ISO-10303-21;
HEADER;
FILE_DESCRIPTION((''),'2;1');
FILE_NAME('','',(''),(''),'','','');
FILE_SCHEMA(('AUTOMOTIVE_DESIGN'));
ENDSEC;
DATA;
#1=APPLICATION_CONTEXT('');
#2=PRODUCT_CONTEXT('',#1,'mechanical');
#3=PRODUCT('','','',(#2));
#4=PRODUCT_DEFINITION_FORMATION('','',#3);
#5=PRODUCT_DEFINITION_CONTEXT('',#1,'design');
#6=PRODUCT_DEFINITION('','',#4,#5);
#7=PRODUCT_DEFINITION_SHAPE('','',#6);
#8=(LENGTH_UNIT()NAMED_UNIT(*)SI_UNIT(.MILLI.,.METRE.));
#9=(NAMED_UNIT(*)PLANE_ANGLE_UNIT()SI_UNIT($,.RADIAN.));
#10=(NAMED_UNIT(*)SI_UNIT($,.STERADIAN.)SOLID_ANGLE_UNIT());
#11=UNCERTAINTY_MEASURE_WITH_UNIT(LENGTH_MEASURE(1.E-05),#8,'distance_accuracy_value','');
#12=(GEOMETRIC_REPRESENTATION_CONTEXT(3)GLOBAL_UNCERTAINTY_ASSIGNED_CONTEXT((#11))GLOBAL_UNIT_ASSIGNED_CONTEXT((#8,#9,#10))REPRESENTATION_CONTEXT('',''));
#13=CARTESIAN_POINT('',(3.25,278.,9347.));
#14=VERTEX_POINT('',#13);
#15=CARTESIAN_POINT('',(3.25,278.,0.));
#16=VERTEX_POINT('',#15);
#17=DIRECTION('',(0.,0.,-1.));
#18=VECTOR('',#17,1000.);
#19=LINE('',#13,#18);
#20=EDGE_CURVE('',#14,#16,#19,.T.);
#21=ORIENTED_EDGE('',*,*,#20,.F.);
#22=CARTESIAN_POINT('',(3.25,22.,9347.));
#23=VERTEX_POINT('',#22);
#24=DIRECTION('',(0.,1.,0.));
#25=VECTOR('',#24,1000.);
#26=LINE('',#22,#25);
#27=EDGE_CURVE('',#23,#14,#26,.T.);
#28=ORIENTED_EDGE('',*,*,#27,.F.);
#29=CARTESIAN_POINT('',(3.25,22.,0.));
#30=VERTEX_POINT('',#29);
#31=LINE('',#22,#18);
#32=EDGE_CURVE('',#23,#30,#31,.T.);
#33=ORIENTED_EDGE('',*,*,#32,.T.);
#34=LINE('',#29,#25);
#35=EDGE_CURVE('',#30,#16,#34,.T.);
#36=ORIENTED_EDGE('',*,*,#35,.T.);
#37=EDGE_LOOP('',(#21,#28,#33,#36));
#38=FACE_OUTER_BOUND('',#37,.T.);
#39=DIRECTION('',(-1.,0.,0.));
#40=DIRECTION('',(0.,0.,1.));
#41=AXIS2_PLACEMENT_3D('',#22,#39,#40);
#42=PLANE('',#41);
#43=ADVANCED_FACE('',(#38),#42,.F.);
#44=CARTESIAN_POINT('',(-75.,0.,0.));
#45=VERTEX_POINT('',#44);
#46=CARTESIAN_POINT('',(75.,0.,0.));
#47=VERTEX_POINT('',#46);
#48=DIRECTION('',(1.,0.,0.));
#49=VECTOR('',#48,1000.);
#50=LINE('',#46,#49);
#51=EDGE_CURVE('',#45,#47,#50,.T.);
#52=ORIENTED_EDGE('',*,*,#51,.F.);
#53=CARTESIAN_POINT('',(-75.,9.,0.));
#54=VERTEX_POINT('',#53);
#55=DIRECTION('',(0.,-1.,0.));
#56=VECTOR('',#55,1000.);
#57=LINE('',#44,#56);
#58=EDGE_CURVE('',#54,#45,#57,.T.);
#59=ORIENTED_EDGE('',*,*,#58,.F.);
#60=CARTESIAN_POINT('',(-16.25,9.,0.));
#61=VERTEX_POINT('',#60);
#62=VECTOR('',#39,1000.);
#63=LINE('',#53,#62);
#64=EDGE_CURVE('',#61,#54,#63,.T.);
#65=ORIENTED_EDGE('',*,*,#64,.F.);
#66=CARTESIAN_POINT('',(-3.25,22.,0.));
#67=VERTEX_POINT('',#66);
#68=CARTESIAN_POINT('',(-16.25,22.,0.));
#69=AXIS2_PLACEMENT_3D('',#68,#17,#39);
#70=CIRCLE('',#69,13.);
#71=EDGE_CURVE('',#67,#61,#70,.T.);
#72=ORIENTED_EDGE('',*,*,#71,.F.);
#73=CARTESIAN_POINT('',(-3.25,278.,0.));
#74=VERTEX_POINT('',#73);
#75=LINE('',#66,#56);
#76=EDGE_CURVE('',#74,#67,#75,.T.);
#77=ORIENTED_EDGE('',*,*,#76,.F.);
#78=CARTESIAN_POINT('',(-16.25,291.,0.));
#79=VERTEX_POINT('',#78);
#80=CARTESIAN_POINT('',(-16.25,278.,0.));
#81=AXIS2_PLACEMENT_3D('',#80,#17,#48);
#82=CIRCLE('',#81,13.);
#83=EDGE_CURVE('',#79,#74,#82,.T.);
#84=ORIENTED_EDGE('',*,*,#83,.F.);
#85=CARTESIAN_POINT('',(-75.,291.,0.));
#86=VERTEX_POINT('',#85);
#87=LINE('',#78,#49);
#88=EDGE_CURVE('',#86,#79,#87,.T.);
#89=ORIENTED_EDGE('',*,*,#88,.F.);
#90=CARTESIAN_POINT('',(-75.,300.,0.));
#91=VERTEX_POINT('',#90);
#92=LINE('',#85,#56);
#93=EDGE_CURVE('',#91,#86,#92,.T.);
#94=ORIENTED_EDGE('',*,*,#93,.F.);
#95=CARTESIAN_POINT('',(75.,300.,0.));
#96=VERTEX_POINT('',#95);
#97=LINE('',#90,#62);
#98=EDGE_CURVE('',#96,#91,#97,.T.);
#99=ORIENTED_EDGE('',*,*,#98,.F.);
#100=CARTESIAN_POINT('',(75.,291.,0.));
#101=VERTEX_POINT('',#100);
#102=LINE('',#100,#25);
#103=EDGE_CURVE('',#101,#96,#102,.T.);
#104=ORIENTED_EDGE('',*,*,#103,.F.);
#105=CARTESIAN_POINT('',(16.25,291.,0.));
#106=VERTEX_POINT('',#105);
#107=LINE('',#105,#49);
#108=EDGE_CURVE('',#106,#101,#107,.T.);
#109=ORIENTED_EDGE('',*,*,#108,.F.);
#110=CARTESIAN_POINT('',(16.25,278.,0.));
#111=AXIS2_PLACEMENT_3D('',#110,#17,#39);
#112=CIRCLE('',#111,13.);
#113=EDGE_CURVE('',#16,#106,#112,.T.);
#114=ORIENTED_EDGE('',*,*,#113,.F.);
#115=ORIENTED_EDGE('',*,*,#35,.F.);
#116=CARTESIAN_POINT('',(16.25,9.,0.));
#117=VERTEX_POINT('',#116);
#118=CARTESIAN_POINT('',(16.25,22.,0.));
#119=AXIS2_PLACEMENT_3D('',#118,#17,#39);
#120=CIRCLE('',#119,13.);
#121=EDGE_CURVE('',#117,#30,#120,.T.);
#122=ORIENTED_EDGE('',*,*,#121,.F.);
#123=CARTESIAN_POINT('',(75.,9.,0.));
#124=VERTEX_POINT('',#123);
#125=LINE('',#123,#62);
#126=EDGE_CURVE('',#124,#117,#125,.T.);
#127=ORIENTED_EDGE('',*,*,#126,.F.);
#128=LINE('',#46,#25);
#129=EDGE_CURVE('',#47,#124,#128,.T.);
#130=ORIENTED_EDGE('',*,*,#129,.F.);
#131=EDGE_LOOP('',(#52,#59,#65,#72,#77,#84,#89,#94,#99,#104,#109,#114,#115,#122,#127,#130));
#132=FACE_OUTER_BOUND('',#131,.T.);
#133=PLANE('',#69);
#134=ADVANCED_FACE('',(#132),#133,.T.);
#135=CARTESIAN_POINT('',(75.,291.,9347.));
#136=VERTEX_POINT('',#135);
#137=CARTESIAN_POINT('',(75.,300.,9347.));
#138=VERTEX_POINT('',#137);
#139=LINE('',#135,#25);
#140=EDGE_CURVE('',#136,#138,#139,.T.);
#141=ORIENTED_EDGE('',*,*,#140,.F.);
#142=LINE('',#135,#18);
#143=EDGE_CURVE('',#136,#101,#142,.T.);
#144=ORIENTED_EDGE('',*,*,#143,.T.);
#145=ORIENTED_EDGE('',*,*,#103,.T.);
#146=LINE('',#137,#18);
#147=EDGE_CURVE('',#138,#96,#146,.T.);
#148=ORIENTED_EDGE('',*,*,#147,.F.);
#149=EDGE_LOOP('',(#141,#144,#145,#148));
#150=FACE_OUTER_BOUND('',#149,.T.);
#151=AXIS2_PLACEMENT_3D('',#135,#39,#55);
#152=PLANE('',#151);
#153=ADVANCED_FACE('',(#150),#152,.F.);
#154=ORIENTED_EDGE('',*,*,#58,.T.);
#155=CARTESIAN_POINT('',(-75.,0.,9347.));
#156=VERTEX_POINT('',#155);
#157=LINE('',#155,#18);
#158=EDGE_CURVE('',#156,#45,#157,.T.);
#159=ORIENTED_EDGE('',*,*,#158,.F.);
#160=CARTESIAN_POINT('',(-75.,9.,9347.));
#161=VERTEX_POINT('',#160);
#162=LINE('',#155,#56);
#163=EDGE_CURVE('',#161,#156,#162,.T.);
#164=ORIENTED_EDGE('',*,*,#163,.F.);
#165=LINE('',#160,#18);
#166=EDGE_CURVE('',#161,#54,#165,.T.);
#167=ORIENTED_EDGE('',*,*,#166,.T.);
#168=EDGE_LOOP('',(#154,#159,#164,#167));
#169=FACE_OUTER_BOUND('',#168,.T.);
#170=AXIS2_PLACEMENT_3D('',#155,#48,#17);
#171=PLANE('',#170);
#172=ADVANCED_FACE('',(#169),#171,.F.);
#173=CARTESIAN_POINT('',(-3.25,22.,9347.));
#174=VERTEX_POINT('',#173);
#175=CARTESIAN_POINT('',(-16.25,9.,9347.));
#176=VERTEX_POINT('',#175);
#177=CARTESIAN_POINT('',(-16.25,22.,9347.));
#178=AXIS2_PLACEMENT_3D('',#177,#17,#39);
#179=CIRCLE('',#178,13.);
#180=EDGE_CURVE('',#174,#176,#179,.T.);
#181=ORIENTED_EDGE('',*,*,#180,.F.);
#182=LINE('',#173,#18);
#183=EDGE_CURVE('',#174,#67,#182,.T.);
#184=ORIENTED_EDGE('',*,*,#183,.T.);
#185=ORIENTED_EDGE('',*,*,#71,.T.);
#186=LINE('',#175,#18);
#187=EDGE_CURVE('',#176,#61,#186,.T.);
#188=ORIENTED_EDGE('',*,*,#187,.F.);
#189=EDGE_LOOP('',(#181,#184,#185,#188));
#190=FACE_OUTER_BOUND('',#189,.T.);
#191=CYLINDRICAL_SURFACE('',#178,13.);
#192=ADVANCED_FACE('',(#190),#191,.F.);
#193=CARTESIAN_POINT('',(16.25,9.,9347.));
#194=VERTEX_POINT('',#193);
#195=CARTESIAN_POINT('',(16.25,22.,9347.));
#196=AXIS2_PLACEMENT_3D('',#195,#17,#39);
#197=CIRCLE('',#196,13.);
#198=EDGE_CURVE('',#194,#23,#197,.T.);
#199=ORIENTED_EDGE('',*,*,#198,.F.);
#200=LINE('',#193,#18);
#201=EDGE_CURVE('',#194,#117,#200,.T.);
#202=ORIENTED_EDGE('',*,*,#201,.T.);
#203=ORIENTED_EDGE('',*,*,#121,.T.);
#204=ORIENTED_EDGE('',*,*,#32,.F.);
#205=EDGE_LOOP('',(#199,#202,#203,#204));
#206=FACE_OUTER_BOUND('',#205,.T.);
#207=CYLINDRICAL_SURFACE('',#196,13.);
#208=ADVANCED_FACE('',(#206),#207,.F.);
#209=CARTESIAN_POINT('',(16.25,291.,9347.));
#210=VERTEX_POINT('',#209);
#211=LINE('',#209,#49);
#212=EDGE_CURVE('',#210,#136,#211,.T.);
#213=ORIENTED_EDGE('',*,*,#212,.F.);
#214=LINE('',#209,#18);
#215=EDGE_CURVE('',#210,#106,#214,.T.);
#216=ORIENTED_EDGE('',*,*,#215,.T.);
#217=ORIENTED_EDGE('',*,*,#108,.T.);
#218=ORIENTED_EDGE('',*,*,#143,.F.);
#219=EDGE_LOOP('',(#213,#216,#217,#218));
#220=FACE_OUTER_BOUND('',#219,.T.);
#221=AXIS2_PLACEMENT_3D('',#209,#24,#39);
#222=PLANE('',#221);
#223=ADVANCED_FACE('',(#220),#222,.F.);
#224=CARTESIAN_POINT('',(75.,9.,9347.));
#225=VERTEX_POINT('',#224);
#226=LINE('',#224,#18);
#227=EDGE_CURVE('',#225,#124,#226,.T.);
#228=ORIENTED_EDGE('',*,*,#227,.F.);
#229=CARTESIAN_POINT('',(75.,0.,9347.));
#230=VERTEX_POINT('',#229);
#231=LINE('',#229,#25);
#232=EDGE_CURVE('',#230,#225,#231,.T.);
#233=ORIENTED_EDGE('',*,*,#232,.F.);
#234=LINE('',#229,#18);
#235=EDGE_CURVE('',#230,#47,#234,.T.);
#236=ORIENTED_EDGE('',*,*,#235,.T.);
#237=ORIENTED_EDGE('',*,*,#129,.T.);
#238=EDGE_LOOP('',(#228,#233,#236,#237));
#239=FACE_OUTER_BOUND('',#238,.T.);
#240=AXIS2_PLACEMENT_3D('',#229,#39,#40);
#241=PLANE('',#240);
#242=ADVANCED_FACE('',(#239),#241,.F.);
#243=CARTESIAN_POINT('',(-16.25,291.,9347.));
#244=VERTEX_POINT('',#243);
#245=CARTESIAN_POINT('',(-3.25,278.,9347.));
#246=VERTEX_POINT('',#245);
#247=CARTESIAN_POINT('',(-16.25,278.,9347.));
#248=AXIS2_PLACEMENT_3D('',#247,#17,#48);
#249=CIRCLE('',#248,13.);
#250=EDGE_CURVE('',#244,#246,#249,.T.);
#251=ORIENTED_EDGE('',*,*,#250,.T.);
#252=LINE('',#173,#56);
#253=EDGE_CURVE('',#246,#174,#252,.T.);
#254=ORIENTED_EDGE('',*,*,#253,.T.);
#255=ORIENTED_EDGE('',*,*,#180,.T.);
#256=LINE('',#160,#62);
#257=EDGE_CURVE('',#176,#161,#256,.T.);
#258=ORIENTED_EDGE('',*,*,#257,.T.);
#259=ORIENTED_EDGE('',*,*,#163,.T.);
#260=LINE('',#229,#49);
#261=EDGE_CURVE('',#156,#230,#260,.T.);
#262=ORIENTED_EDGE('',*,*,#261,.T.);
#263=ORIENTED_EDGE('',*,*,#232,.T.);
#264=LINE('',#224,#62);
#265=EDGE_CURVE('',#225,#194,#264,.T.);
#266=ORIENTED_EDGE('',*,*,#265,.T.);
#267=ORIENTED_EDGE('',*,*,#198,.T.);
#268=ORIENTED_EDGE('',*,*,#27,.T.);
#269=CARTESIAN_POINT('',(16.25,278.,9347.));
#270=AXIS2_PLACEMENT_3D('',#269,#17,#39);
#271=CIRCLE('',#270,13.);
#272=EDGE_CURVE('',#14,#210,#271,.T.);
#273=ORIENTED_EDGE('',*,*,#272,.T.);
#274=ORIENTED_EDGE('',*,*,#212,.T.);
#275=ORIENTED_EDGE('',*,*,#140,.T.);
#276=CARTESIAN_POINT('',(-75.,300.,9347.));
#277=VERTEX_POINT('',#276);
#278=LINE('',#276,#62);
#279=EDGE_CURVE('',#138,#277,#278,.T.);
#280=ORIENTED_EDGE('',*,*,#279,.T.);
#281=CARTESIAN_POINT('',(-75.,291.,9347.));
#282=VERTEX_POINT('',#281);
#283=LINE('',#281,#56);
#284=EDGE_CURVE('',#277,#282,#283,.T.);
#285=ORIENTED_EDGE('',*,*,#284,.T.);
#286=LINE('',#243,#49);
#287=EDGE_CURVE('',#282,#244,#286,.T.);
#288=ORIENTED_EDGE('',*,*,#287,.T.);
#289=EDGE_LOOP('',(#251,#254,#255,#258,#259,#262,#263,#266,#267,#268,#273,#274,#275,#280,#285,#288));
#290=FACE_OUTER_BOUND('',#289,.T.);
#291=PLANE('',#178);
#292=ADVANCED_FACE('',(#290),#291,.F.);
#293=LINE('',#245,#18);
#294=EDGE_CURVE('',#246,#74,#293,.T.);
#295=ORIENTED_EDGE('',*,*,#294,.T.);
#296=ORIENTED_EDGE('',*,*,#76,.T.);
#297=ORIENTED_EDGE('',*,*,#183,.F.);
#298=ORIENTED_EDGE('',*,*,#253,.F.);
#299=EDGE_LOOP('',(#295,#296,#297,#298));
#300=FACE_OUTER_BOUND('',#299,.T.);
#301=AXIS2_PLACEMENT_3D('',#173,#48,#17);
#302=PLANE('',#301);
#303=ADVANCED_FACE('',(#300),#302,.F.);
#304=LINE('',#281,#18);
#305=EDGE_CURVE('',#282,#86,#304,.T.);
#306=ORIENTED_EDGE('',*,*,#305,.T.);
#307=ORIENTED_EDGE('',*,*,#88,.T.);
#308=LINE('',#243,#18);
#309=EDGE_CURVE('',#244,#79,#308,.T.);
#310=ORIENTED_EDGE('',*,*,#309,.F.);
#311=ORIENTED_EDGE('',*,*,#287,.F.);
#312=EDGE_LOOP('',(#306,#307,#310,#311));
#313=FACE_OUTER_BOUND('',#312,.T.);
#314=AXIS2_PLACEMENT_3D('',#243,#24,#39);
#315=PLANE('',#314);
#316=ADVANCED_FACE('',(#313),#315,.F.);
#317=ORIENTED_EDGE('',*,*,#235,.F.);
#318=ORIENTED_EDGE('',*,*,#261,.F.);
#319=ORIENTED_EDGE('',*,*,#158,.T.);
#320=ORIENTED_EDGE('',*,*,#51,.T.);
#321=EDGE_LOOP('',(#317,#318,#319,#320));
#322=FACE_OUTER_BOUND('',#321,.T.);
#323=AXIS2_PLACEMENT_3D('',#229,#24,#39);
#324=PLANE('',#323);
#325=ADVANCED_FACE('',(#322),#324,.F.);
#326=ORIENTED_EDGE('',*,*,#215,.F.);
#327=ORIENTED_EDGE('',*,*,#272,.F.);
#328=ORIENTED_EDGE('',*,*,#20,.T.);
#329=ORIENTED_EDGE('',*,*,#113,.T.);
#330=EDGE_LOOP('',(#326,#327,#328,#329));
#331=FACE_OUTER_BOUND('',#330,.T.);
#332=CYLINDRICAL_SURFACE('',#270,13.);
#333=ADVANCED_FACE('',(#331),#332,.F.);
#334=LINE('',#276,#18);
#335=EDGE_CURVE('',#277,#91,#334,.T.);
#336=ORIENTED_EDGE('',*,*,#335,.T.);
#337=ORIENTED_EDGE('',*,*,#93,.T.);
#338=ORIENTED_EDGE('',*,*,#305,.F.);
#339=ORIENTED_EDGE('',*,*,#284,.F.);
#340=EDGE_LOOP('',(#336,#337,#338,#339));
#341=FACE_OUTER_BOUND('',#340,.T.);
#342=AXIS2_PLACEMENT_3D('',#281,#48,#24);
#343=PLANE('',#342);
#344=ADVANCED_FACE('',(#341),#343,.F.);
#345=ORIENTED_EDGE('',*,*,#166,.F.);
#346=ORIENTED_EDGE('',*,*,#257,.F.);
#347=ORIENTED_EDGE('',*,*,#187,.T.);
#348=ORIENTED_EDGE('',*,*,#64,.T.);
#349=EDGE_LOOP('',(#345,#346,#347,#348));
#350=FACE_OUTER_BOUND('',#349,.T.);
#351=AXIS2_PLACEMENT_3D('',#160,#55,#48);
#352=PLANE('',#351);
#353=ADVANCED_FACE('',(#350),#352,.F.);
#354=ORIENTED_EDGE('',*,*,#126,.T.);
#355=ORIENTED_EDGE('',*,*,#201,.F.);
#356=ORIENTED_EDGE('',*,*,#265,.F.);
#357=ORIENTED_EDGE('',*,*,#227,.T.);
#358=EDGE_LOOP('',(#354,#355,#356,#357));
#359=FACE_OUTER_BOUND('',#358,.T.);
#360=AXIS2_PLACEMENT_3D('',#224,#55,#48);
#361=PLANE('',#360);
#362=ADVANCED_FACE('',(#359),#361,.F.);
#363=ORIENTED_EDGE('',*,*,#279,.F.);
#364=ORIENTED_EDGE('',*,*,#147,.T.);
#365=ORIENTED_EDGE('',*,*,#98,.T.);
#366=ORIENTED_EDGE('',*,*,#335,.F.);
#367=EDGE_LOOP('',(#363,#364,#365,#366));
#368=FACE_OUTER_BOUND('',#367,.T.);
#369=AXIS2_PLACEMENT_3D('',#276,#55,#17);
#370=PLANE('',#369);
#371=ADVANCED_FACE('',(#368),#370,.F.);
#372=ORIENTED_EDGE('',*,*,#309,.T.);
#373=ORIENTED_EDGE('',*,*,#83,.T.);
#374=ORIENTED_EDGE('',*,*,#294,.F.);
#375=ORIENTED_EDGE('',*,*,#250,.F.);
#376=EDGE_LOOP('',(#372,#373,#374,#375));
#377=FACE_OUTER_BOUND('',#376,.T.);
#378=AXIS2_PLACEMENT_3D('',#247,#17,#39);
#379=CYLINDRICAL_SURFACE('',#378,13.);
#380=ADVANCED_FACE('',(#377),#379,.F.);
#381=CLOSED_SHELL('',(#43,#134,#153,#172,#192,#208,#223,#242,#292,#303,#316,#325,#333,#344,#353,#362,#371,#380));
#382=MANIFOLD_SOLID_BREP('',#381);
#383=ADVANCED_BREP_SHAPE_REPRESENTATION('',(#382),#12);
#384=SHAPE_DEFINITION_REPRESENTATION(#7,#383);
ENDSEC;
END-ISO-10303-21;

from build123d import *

# Parameters (mm, degrees)
BOSS_EXTRUDE1_DEPTH = 9347


with BuildPart() as part:
    # Sketch1 → Boss-Extrude1 (new body)
    with BuildSketch(Plane.XY):
        with BuildLine():
            Line((75, 0), (-75, 0))
            Line((-75, 0), (-75, 9))
            Line((-75, 9), (-16.25, 9))
            ThreePointArc((-16.25, 9), (-7.057611845, 12.807611845), (-3.25, 22))
            Line((-3.25, 22), (-3.25, 278))
            ThreePointArc((-3.25, 278), (-7.057611845, 287.192388155), (-16.25, 291))
            Line((-16.25, 291), (-75, 291))
            Line((-75, 291), (-75, 300))
            Line((-75, 300), (75, 300))
            Line((75, 300), (75, 291))
            Line((75, 291), (16.25, 291))
            ThreePointArc((16.25, 291), (7.057611845, 287.192388155), (3.25, 278))
            Line((3.25, 278), (3.25, 22))
            ThreePointArc((3.25, 22), (7.057611845, 12.807611845), (16.25, 9))
            Line((16.25, 9), (75, 9))
            Line((75, 9), (75, 0))
        make_face()
    extrude(amount=BOSS_EXTRUDE1_DEPTH)


solid = part.part
